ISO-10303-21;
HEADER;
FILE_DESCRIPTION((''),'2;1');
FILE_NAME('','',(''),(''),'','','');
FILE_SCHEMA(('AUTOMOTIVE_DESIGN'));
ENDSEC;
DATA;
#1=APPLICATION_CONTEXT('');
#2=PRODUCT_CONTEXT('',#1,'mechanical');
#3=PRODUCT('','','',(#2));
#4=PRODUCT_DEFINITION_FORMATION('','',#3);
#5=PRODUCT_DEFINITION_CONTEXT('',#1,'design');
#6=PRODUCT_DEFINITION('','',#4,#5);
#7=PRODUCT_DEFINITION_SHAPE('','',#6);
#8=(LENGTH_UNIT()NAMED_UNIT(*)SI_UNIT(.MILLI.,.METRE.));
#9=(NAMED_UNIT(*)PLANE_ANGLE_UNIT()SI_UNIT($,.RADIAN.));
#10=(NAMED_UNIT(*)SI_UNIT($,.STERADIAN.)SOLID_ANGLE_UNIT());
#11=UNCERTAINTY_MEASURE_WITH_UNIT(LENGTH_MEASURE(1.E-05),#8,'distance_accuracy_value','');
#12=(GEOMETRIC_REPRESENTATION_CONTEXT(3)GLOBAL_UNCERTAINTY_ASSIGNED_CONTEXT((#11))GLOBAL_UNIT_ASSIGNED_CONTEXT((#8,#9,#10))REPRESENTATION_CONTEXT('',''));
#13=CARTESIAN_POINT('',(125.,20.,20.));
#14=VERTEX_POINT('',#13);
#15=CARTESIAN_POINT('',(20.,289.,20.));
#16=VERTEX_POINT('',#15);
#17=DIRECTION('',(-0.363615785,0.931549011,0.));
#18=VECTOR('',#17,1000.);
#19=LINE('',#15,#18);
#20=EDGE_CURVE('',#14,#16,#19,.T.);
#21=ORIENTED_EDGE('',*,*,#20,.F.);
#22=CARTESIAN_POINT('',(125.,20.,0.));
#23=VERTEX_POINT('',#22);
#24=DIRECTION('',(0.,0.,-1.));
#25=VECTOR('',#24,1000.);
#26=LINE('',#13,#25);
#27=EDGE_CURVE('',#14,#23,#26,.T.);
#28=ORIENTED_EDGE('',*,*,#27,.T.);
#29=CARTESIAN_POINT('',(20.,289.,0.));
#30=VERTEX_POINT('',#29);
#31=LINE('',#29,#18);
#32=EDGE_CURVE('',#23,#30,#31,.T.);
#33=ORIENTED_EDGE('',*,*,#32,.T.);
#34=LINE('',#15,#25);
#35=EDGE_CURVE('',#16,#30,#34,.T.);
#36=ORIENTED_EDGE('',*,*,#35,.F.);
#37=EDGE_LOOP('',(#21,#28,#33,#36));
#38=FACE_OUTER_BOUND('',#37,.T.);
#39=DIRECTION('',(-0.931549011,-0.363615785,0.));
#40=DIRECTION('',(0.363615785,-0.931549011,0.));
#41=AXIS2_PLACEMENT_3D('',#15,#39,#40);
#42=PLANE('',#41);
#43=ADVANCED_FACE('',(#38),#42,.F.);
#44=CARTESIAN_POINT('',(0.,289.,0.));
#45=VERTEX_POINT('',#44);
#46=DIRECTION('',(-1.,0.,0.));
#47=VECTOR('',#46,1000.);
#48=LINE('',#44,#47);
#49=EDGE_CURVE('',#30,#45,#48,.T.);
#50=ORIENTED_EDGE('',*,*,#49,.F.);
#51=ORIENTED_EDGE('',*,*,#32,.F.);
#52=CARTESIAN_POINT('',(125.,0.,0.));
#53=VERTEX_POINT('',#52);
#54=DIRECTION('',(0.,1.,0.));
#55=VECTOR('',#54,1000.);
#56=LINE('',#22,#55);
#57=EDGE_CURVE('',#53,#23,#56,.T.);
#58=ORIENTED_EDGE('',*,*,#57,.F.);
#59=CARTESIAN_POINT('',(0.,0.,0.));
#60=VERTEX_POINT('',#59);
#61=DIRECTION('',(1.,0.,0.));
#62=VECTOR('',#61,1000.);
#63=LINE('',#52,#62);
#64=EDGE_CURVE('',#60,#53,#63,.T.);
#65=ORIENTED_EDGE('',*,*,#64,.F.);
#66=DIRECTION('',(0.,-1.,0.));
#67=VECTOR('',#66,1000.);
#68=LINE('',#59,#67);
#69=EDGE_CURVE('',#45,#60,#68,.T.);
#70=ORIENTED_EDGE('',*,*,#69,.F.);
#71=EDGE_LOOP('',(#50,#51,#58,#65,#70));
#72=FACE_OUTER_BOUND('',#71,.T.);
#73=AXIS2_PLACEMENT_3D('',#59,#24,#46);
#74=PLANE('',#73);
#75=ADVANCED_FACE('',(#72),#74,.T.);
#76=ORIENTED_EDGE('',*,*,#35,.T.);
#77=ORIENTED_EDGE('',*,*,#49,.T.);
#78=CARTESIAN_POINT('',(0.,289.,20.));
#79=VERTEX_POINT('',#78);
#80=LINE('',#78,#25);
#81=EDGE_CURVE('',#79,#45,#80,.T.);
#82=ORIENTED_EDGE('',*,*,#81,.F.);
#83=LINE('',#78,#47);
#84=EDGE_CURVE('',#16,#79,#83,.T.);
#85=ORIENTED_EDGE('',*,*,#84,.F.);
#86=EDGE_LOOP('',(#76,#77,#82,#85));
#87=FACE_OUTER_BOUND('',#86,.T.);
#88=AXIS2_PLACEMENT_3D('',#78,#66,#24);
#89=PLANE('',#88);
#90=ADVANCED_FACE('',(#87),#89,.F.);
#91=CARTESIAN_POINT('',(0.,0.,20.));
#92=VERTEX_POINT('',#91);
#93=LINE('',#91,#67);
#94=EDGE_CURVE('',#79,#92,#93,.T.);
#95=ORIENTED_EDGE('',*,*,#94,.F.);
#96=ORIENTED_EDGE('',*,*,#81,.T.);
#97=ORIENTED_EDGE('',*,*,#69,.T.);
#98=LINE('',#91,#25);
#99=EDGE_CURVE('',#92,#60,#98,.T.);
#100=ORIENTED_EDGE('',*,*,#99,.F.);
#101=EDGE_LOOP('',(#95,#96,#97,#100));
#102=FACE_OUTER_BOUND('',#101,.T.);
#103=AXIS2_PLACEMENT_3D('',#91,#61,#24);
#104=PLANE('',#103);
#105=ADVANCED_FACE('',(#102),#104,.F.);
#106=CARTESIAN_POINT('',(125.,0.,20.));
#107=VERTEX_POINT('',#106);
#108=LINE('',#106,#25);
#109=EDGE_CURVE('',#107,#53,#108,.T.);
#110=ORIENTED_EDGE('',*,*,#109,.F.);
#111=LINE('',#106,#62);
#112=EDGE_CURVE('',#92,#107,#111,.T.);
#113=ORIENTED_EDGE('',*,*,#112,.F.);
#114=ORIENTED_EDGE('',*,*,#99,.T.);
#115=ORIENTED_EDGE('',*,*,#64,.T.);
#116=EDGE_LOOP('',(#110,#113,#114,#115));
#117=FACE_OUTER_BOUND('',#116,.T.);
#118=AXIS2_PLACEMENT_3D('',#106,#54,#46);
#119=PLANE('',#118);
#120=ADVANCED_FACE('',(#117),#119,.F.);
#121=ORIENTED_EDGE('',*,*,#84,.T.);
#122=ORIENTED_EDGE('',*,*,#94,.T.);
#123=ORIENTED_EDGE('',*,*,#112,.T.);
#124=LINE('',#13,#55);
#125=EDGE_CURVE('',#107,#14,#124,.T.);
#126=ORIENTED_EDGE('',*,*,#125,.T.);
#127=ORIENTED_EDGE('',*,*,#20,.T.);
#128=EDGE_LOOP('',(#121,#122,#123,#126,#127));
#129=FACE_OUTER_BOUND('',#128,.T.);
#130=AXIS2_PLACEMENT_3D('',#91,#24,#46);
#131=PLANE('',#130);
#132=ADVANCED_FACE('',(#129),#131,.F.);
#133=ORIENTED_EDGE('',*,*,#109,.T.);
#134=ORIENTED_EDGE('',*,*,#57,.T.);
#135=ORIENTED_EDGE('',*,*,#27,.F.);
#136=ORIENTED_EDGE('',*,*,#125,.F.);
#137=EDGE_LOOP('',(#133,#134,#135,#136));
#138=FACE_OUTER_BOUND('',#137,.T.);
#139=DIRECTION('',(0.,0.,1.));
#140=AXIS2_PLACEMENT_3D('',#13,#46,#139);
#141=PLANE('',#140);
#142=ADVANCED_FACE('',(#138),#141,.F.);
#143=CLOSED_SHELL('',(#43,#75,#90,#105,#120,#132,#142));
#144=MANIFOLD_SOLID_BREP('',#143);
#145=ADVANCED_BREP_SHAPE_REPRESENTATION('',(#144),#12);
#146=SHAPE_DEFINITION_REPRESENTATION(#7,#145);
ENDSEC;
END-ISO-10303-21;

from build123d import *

# Parameters (mm, degrees)
BOSS_EXTRUDE1_DEPTH = 20


with BuildPart() as part:
    # Sketch1 → Boss-Extrude1 (new body)
    with BuildSketch(Plane.XY):
        Polygon((0, 0), (0, 289), (20, 289), (125, 20), (125, 0), align=None)
    extrude(amount=BOSS_EXTRUDE1_DEPTH)


solid = part.part
